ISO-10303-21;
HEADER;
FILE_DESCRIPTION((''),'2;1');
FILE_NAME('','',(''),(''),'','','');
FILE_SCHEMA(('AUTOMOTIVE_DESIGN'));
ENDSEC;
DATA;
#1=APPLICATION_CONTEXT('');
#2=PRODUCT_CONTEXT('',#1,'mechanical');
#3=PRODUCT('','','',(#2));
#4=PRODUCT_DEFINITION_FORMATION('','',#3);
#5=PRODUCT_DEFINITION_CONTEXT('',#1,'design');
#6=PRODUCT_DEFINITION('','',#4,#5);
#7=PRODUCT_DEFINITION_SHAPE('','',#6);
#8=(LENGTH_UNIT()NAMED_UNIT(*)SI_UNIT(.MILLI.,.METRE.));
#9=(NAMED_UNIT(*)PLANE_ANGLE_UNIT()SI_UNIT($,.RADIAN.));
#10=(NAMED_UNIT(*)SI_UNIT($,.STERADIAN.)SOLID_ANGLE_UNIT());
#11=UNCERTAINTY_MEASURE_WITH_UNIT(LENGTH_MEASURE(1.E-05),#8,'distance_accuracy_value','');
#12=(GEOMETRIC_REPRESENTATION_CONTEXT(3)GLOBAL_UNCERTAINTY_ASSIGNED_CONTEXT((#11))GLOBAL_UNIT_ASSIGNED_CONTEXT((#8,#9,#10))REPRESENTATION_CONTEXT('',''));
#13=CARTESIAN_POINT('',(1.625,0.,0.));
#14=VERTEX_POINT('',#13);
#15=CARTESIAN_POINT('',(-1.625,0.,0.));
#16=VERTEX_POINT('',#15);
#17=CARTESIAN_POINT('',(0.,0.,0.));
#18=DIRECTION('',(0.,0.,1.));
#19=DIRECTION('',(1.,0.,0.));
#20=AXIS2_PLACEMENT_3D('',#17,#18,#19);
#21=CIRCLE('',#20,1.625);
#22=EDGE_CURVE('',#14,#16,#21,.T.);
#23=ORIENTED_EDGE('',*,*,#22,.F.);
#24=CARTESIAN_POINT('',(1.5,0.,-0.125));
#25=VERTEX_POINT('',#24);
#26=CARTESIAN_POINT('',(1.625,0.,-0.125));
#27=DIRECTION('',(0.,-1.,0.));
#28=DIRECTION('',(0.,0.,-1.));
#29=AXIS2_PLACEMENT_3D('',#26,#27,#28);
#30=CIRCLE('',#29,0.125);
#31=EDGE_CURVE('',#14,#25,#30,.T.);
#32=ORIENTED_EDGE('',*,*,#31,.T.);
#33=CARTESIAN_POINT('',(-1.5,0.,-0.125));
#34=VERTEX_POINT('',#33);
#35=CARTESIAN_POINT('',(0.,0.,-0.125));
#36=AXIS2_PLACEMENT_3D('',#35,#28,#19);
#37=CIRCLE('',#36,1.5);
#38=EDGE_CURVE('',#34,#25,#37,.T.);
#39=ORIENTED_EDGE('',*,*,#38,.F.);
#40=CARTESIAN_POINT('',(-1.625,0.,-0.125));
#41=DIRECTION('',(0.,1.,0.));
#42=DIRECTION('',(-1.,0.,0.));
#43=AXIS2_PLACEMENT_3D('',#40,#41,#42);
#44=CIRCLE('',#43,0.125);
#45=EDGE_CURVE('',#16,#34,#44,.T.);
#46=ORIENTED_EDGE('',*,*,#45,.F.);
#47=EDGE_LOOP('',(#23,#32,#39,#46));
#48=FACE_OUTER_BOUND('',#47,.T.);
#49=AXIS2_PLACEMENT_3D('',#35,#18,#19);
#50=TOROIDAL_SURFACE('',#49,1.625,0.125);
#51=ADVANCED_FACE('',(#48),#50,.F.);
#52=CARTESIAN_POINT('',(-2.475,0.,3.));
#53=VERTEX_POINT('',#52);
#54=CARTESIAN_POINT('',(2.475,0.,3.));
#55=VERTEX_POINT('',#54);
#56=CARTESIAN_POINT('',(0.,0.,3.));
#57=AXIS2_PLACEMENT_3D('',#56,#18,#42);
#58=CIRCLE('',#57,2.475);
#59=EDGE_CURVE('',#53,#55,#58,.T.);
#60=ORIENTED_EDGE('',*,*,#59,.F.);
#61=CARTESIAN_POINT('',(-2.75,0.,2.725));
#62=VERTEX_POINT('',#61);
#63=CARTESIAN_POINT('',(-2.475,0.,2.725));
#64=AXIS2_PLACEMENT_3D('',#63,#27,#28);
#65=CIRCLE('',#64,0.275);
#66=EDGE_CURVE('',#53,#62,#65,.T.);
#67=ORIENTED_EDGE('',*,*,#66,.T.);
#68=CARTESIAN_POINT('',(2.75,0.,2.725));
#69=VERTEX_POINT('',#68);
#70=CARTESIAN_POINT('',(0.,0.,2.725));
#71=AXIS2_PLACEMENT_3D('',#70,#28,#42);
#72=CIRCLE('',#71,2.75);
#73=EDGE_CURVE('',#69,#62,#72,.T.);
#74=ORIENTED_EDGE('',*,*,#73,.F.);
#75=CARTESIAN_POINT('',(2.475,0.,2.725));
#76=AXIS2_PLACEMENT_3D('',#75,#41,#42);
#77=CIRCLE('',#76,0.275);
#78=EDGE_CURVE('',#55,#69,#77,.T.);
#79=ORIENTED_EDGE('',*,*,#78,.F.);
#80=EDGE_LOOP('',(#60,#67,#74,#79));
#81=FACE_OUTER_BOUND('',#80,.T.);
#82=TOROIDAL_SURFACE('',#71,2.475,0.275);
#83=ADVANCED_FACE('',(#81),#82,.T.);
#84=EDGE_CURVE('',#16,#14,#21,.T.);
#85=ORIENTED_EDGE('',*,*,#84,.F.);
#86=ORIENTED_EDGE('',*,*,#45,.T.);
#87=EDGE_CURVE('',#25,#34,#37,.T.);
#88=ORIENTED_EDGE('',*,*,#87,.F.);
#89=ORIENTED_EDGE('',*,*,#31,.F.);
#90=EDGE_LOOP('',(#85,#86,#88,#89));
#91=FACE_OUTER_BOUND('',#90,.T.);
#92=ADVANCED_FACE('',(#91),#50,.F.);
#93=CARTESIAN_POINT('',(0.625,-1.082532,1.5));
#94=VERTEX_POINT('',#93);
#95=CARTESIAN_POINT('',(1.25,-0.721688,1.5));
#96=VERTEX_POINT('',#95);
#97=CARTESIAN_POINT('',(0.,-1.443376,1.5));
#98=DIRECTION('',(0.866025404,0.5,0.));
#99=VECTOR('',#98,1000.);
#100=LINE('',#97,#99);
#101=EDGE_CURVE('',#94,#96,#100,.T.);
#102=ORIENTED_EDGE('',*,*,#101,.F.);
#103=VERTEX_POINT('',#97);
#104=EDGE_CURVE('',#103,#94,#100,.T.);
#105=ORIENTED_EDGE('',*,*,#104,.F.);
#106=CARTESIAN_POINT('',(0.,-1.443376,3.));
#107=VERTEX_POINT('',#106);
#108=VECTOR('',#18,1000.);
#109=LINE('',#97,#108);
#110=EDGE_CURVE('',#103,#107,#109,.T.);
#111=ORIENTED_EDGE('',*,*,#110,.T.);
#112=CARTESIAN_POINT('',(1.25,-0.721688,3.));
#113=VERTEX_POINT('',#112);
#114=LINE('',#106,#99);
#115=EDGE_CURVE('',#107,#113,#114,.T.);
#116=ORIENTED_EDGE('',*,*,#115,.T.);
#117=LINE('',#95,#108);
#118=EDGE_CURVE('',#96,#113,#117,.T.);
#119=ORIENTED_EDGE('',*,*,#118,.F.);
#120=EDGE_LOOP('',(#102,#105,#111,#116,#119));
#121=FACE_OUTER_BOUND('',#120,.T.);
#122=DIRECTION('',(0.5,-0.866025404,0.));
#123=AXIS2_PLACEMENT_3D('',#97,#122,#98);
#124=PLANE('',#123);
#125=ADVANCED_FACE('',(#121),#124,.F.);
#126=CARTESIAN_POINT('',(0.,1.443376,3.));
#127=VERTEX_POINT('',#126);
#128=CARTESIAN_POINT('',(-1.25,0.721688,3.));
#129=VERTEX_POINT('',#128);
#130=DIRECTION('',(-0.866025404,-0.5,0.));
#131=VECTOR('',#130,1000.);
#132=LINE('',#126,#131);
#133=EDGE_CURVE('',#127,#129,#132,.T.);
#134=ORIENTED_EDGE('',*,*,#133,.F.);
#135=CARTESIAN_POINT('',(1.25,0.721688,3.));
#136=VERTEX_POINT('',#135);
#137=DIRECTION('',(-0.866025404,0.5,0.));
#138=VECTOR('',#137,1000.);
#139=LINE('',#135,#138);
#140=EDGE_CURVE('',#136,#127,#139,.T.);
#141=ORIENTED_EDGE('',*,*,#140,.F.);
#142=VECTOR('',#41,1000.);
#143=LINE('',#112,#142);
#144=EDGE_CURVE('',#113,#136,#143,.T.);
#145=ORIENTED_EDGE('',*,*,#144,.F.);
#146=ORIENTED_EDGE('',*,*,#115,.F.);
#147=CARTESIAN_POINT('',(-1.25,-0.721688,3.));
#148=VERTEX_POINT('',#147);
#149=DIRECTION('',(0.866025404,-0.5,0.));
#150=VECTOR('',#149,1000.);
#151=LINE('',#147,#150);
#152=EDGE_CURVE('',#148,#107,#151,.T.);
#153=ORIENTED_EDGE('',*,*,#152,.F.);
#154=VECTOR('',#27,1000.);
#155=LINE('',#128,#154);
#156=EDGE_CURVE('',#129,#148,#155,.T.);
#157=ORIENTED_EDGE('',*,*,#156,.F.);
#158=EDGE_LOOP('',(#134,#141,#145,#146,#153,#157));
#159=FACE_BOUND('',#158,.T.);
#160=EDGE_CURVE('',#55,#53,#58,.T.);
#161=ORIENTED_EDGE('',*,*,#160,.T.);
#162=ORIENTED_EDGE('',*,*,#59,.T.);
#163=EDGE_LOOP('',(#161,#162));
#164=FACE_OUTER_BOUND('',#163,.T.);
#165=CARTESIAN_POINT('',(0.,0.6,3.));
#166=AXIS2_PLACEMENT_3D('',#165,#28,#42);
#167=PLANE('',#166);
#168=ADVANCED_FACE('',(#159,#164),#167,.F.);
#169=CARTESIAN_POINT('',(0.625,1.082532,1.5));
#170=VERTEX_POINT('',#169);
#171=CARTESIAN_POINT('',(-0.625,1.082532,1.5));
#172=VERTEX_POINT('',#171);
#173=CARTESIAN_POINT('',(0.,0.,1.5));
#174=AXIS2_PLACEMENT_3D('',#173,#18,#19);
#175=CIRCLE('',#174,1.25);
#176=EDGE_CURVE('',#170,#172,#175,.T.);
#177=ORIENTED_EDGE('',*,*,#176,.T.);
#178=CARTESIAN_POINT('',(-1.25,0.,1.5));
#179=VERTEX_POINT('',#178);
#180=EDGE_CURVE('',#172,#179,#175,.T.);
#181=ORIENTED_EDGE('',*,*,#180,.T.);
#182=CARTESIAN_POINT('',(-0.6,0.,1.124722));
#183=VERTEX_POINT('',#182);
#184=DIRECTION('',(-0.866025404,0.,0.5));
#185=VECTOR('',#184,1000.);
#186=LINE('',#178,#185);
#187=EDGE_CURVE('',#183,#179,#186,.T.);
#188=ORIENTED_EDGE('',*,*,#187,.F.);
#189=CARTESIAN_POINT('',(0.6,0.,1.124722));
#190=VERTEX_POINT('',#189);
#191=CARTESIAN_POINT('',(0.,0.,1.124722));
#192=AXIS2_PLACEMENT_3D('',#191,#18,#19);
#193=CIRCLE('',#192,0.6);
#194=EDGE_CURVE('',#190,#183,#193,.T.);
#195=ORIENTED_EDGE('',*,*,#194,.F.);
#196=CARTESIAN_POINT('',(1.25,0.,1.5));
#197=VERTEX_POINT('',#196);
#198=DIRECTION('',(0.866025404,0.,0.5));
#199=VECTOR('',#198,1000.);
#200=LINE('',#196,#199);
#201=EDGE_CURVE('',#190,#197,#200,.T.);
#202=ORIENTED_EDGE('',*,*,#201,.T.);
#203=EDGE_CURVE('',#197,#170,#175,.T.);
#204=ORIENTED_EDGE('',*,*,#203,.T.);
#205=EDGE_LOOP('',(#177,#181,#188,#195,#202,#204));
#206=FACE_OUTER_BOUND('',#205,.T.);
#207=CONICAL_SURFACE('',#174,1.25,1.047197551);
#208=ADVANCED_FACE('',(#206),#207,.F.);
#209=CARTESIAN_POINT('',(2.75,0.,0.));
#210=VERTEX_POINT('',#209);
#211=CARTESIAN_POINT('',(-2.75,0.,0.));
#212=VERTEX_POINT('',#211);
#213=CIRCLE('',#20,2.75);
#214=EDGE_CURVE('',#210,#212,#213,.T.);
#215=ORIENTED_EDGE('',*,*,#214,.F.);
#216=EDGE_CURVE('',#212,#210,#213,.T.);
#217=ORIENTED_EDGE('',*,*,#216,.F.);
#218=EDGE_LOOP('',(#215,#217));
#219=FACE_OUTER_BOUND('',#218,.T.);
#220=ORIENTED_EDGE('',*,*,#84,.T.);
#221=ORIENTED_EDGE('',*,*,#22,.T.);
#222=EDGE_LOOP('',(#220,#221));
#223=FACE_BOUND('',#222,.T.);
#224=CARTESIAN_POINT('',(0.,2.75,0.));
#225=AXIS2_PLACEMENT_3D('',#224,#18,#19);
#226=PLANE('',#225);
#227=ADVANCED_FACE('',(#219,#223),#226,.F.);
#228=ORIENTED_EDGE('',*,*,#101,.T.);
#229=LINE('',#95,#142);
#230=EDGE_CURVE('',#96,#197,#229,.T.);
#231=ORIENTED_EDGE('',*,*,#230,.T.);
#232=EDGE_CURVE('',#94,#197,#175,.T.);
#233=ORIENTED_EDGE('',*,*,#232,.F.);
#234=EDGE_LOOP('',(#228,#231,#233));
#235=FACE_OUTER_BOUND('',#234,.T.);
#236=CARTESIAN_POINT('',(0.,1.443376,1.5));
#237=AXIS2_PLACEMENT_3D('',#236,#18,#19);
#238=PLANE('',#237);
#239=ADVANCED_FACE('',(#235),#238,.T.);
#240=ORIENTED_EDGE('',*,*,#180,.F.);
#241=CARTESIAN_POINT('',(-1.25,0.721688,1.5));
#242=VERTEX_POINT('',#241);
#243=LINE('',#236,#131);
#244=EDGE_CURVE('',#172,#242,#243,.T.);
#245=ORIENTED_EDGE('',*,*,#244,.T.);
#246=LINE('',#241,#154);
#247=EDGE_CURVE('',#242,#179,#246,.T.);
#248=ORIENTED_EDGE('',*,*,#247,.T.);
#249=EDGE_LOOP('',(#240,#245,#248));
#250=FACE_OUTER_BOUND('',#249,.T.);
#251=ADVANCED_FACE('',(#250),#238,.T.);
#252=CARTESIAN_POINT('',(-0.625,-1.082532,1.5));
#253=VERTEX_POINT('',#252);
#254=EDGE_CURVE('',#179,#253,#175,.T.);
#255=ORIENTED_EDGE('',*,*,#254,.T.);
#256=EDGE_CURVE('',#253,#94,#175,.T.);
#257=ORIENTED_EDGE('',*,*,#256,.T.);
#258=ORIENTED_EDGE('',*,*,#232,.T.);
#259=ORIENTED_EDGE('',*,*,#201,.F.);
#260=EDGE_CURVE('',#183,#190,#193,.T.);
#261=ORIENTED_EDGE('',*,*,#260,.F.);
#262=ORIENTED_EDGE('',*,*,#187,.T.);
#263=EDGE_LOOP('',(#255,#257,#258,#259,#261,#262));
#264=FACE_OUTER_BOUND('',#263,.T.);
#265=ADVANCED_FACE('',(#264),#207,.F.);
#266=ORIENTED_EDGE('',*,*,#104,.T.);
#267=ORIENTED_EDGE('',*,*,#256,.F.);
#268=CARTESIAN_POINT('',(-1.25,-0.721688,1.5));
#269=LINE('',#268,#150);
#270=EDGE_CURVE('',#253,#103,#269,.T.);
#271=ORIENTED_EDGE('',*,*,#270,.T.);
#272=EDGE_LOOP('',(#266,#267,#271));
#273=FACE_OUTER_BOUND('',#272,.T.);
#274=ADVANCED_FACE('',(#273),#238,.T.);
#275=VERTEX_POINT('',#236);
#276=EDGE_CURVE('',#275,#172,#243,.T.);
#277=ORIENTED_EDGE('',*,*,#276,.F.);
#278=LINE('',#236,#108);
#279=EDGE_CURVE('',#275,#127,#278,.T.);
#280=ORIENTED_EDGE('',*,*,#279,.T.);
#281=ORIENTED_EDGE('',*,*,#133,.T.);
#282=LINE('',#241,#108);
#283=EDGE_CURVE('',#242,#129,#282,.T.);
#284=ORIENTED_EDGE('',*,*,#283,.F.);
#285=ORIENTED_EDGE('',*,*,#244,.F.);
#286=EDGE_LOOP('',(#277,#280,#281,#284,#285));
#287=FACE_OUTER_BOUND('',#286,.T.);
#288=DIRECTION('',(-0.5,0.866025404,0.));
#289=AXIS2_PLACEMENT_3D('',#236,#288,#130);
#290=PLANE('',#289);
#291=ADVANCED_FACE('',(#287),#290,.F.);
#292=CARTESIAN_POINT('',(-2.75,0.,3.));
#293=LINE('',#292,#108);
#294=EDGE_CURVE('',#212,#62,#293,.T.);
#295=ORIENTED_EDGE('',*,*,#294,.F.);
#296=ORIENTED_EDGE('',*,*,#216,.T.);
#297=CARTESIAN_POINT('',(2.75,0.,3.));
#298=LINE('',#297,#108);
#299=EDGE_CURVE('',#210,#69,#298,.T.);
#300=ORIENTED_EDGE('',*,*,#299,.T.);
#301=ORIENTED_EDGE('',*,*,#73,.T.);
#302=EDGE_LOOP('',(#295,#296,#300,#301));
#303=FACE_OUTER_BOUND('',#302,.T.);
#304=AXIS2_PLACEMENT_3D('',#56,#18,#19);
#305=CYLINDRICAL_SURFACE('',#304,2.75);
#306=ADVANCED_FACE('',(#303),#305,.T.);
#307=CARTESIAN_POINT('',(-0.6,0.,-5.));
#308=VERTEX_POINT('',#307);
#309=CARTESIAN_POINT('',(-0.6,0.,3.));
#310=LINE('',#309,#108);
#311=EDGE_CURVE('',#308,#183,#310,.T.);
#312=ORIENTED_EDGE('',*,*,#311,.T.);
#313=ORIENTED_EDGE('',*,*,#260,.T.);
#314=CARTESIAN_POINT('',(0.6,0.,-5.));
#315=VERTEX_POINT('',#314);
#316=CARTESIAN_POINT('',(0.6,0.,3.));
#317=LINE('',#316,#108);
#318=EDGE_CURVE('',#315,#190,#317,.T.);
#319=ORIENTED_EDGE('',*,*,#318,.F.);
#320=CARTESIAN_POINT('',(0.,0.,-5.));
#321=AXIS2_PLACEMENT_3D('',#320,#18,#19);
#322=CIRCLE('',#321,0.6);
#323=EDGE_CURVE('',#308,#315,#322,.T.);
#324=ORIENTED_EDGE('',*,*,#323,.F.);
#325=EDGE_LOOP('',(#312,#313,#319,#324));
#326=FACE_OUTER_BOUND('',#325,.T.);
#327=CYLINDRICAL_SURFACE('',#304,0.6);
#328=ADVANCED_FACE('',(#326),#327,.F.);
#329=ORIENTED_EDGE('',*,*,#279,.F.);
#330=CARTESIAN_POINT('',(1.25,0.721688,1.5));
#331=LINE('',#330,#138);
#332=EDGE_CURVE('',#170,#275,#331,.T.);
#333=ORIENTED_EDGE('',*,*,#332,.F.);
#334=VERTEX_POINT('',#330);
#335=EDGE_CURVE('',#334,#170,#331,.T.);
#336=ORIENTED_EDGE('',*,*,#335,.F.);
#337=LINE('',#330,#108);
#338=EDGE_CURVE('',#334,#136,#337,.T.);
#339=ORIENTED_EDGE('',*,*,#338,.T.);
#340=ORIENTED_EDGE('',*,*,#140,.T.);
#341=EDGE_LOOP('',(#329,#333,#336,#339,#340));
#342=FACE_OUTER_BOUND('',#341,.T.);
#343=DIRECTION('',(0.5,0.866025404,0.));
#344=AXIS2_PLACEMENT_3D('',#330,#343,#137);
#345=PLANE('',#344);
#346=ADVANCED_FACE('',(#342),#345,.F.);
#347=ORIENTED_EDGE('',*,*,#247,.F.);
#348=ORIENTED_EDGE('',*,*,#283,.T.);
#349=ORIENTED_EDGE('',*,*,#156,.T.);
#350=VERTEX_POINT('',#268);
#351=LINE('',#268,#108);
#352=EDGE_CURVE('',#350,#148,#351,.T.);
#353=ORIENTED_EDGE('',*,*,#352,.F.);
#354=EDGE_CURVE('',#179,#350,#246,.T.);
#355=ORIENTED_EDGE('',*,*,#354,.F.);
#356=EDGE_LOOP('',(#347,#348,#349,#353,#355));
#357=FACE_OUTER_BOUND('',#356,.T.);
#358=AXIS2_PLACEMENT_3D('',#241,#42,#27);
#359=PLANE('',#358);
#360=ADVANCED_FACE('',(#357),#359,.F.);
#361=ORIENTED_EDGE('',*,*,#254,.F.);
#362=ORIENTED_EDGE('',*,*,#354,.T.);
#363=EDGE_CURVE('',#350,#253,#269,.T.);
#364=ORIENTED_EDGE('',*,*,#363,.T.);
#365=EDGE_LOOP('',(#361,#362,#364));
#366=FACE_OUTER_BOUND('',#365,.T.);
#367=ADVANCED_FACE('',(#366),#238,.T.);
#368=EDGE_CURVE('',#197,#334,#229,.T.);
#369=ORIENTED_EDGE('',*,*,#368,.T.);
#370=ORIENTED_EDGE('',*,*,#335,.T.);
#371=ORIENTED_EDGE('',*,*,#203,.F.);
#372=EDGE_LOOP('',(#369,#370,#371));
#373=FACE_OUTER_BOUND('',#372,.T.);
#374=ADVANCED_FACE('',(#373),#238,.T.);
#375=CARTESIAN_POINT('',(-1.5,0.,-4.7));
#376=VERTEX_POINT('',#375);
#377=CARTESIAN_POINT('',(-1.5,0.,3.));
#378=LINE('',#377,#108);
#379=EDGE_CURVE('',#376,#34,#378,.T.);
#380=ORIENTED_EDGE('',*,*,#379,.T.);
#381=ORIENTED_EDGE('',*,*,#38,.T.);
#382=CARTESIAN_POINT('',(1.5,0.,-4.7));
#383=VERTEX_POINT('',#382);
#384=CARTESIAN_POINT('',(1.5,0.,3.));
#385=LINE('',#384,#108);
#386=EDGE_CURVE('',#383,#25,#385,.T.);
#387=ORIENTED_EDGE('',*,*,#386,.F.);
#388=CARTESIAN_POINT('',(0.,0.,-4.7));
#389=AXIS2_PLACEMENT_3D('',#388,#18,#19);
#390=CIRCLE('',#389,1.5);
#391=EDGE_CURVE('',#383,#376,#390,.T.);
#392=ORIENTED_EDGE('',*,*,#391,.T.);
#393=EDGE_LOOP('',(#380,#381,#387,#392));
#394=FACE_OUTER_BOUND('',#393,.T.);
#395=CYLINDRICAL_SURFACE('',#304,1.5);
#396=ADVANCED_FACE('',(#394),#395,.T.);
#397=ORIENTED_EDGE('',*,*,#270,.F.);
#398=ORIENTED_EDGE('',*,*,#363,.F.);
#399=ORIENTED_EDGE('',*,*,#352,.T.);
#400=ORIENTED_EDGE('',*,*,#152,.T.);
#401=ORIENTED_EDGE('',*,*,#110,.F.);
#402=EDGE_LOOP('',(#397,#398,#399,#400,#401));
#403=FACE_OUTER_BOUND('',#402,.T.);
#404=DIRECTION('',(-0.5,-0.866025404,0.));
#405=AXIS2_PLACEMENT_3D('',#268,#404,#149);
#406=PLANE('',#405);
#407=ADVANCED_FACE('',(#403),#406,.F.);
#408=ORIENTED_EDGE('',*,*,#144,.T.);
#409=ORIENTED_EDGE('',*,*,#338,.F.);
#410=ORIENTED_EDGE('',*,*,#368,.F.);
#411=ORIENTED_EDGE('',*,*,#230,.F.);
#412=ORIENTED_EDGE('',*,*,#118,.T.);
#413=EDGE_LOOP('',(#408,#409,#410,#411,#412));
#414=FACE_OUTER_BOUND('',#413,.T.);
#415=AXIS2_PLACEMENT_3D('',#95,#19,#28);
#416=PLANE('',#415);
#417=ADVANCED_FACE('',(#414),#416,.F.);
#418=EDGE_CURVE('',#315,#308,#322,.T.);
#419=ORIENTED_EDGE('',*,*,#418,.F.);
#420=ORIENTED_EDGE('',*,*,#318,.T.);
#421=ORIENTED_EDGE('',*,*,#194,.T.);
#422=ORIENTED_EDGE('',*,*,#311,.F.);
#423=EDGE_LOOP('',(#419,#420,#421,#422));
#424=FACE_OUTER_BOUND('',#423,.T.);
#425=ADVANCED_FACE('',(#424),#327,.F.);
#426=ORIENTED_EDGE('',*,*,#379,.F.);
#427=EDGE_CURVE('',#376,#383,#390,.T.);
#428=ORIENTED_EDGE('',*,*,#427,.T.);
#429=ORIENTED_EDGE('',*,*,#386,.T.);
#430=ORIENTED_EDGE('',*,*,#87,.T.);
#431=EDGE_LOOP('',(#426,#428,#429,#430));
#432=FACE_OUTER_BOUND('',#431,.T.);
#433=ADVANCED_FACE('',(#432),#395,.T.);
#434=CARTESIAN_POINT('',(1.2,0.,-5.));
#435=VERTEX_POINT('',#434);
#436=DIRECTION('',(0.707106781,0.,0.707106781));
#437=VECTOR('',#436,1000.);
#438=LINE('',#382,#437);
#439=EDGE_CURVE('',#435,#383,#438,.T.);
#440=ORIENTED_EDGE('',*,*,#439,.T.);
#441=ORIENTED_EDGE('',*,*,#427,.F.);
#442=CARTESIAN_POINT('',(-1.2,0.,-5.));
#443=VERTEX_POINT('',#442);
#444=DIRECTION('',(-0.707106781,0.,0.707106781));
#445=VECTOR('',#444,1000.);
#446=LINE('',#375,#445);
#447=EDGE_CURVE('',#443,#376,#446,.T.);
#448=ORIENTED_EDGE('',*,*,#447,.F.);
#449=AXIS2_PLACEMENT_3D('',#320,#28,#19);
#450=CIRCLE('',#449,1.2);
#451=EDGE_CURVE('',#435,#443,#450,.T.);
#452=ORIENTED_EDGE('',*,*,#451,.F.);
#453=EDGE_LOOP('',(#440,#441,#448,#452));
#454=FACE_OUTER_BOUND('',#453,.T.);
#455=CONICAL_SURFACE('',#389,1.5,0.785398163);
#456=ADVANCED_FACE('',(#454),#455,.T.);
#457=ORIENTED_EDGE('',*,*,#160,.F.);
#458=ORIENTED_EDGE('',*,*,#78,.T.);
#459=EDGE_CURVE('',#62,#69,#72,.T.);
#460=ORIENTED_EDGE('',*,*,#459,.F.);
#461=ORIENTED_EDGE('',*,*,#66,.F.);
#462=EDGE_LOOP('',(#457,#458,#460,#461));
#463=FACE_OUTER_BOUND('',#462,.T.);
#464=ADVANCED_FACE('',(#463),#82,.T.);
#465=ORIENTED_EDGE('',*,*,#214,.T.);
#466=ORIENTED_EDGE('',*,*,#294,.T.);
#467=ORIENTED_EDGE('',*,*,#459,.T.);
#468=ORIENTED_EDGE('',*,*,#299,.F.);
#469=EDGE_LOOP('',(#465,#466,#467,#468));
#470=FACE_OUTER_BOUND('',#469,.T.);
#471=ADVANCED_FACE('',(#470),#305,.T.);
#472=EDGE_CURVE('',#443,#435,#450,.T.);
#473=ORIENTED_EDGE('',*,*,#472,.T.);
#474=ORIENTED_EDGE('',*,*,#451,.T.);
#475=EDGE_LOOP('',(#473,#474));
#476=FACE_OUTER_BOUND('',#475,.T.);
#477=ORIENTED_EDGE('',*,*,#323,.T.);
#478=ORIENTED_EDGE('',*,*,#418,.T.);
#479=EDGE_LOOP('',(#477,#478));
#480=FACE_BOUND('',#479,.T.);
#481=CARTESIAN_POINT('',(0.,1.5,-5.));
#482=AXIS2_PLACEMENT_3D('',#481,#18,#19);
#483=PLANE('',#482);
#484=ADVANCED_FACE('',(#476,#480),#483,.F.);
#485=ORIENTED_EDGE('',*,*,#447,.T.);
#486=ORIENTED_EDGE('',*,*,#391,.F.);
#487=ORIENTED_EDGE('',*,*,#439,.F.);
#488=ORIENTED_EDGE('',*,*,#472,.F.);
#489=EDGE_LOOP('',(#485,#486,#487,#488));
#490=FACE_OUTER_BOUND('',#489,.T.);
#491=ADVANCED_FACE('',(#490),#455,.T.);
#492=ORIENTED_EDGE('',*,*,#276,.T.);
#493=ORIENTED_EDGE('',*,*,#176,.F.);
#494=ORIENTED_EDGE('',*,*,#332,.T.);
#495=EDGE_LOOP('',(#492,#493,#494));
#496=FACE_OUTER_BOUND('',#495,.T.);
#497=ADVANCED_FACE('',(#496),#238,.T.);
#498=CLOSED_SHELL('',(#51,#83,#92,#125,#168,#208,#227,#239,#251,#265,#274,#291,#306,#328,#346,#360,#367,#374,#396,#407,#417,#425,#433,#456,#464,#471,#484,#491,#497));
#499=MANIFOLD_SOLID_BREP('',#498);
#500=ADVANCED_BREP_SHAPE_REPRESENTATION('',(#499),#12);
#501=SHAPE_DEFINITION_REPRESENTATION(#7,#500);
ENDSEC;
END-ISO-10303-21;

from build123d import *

# Parameters (mm, degrees)
CUT_EXTRUDE1_DEPTH = 1.5
FILLET1_R          = 0.275
CHAMFER1_SIZE      = 0.3
FILLET2_R          = 0.125


with BuildPart() as part:
    # Sketch3 → Revolve1 (revolve)
    with BuildSketch(Plane(origin=(0, 0, 0), x_dir=(0, 0, -1), z_dir=(1, 0, 0)), mode=Mode.PRIVATE) as revolve1_sk:
        Polygon((-3, 0.6), (-3, 2.75), (0, 2.75), (0, 1.5), (5, 1.5), (5, 0.6), align=None)
    revolve(revolve1_sk.sketch.rotate(Axis((0, 0, 3), (0, 0, -1)), 90), axis=Axis((0, 0, 3), (0, 0, -1)))

    # Sketch4 → Cut-Extrude1 (cut)
    with BuildSketch(Plane.XY.offset(3)):
        Polygon((0, 1.443375673), (-1.25, 0.721687836), (-1.25, -0.721687836), (0, -1.443375673), (1.25, -0.721687836), (1.25, 0.721687836), align=None)
    extrude(amount=-CUT_EXTRUDE1_DEPTH, mode=Mode.SUBTRACT)

    # Fillet1
    fillet1_edges = [part.edges().sort_by_distance(p)[0] for p in [
        (-2.75, 0, 3),
    ]]
    fillet(fillet1_edges, radius=FILLET1_R)

    # Chamfer1
    chamfer1_edges = [part.edges().sort_by_distance(p)[0] for p in [
        (-1.5, 0, -5),
    ]]
    chamfer(chamfer1_edges, length=CHAMFER1_SIZE)

    # Cut-Extrude2 cone 1 section (through the dimple's axis) → Cut-Extrude2 (revolve, cut)
    with BuildSketch(Plane(origin=(0, 0, 1.5), x_dir=(0, -1, 0), z_dir=(1, 0, 0))):
        Polygon((0, 0), (1.25, 0), (0, 0.721687836), align=None)
    revolve(axis=Axis((0, 0, 1.5), (0, 0, -1)), mode=Mode.SUBTRACT)

    # Fillet2
    fillet2_edges = [part.edges().sort_by_distance(p)[0] for p in [
        (-1.5, 0, 0),
    ]]
    fillet(fillet2_edges, radius=FILLET2_R)


solid = part.part
